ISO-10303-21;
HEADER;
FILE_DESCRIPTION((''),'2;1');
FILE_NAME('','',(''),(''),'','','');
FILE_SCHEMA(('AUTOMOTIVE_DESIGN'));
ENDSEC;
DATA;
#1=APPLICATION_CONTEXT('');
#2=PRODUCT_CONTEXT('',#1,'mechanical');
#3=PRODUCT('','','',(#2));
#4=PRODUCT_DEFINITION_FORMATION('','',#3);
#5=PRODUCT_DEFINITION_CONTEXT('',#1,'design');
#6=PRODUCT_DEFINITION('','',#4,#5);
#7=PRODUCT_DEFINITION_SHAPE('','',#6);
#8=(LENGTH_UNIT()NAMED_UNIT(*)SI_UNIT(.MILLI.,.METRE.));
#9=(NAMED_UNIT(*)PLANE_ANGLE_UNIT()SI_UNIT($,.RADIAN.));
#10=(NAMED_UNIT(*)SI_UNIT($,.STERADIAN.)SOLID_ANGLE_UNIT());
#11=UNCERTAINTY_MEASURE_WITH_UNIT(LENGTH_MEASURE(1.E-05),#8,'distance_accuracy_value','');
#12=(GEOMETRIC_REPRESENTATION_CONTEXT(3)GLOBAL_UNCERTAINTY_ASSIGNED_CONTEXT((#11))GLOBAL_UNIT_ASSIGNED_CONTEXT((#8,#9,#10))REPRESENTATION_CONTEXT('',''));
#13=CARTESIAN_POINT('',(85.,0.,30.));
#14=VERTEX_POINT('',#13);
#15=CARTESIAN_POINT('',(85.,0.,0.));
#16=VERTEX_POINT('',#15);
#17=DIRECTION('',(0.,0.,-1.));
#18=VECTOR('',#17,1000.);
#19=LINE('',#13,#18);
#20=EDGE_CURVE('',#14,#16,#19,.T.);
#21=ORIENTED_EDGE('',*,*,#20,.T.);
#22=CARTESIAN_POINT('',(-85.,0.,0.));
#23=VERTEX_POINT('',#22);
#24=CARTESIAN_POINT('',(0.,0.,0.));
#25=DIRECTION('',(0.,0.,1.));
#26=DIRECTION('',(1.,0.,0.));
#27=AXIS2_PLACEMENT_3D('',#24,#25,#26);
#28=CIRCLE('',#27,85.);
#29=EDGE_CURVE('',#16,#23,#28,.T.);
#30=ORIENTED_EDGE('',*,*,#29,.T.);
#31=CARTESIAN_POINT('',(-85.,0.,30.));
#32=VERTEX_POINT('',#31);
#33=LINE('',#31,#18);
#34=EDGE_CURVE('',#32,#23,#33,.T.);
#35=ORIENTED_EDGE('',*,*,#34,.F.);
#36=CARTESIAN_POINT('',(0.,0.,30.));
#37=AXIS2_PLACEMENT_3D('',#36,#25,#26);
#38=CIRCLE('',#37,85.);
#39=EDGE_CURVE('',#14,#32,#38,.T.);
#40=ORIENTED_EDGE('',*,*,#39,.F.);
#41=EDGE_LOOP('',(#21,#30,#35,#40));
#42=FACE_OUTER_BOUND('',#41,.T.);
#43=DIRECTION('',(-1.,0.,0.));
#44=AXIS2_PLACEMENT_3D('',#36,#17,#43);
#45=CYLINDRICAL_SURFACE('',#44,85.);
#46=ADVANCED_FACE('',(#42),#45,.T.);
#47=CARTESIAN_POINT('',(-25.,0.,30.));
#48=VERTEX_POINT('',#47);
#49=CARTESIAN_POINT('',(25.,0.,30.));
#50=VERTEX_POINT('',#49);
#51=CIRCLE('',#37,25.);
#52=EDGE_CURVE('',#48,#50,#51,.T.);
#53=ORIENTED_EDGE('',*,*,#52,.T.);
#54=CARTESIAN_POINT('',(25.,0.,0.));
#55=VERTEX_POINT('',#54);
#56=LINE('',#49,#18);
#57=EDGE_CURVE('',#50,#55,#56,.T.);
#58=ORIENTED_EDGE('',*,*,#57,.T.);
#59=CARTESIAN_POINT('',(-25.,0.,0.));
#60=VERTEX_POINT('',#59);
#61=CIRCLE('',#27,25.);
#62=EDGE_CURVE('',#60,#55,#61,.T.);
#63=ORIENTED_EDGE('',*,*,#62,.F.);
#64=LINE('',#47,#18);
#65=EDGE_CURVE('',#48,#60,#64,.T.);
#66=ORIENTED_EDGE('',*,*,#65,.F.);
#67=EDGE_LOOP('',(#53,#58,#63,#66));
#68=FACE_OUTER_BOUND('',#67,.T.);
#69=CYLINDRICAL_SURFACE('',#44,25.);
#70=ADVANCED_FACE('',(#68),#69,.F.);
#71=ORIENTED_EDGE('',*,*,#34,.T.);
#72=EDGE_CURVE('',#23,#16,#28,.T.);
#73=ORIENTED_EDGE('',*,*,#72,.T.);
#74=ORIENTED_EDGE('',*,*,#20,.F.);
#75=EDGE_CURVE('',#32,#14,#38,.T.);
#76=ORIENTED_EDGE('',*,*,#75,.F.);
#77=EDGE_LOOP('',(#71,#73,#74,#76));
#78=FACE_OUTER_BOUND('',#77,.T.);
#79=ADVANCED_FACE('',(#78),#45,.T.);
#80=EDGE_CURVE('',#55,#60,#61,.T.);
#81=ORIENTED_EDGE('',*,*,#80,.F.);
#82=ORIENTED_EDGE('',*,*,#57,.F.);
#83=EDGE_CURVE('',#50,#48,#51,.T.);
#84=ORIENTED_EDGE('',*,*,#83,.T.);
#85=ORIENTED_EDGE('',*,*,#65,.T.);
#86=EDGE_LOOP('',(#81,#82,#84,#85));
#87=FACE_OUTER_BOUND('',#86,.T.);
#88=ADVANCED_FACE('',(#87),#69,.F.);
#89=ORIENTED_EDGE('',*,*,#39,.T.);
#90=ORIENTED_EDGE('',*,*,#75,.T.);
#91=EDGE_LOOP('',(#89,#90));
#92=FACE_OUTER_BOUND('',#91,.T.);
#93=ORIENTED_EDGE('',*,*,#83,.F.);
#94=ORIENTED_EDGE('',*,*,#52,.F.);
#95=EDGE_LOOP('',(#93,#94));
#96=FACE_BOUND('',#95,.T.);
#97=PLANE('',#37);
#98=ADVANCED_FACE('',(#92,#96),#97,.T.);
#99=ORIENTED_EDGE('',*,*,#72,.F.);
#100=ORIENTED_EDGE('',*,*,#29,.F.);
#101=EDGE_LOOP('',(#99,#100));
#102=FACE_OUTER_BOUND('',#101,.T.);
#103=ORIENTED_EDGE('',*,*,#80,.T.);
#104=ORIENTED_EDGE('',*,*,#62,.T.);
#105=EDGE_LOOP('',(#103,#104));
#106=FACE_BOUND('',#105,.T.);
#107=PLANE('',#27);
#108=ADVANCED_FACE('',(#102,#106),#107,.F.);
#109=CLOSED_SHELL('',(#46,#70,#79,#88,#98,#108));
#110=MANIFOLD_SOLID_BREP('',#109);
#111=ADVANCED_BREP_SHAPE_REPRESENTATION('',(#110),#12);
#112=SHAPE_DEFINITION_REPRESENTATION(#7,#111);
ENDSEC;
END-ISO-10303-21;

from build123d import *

# Parameters (mm, degrees)
SKETCH1_R           = 85
SKETCH1_R_2         = 25
BOSS_EXTRUDE1_DEPTH = 30


with BuildPart() as part:
    # Sketch1 → Boss-Extrude1 (new body)
    with BuildSketch(Plane.XY):
        Circle(SKETCH1_R)
        Circle(SKETCH1_R_2, mode=Mode.SUBTRACT)
    extrude(amount=BOSS_EXTRUDE1_DEPTH)


solid = part.part
